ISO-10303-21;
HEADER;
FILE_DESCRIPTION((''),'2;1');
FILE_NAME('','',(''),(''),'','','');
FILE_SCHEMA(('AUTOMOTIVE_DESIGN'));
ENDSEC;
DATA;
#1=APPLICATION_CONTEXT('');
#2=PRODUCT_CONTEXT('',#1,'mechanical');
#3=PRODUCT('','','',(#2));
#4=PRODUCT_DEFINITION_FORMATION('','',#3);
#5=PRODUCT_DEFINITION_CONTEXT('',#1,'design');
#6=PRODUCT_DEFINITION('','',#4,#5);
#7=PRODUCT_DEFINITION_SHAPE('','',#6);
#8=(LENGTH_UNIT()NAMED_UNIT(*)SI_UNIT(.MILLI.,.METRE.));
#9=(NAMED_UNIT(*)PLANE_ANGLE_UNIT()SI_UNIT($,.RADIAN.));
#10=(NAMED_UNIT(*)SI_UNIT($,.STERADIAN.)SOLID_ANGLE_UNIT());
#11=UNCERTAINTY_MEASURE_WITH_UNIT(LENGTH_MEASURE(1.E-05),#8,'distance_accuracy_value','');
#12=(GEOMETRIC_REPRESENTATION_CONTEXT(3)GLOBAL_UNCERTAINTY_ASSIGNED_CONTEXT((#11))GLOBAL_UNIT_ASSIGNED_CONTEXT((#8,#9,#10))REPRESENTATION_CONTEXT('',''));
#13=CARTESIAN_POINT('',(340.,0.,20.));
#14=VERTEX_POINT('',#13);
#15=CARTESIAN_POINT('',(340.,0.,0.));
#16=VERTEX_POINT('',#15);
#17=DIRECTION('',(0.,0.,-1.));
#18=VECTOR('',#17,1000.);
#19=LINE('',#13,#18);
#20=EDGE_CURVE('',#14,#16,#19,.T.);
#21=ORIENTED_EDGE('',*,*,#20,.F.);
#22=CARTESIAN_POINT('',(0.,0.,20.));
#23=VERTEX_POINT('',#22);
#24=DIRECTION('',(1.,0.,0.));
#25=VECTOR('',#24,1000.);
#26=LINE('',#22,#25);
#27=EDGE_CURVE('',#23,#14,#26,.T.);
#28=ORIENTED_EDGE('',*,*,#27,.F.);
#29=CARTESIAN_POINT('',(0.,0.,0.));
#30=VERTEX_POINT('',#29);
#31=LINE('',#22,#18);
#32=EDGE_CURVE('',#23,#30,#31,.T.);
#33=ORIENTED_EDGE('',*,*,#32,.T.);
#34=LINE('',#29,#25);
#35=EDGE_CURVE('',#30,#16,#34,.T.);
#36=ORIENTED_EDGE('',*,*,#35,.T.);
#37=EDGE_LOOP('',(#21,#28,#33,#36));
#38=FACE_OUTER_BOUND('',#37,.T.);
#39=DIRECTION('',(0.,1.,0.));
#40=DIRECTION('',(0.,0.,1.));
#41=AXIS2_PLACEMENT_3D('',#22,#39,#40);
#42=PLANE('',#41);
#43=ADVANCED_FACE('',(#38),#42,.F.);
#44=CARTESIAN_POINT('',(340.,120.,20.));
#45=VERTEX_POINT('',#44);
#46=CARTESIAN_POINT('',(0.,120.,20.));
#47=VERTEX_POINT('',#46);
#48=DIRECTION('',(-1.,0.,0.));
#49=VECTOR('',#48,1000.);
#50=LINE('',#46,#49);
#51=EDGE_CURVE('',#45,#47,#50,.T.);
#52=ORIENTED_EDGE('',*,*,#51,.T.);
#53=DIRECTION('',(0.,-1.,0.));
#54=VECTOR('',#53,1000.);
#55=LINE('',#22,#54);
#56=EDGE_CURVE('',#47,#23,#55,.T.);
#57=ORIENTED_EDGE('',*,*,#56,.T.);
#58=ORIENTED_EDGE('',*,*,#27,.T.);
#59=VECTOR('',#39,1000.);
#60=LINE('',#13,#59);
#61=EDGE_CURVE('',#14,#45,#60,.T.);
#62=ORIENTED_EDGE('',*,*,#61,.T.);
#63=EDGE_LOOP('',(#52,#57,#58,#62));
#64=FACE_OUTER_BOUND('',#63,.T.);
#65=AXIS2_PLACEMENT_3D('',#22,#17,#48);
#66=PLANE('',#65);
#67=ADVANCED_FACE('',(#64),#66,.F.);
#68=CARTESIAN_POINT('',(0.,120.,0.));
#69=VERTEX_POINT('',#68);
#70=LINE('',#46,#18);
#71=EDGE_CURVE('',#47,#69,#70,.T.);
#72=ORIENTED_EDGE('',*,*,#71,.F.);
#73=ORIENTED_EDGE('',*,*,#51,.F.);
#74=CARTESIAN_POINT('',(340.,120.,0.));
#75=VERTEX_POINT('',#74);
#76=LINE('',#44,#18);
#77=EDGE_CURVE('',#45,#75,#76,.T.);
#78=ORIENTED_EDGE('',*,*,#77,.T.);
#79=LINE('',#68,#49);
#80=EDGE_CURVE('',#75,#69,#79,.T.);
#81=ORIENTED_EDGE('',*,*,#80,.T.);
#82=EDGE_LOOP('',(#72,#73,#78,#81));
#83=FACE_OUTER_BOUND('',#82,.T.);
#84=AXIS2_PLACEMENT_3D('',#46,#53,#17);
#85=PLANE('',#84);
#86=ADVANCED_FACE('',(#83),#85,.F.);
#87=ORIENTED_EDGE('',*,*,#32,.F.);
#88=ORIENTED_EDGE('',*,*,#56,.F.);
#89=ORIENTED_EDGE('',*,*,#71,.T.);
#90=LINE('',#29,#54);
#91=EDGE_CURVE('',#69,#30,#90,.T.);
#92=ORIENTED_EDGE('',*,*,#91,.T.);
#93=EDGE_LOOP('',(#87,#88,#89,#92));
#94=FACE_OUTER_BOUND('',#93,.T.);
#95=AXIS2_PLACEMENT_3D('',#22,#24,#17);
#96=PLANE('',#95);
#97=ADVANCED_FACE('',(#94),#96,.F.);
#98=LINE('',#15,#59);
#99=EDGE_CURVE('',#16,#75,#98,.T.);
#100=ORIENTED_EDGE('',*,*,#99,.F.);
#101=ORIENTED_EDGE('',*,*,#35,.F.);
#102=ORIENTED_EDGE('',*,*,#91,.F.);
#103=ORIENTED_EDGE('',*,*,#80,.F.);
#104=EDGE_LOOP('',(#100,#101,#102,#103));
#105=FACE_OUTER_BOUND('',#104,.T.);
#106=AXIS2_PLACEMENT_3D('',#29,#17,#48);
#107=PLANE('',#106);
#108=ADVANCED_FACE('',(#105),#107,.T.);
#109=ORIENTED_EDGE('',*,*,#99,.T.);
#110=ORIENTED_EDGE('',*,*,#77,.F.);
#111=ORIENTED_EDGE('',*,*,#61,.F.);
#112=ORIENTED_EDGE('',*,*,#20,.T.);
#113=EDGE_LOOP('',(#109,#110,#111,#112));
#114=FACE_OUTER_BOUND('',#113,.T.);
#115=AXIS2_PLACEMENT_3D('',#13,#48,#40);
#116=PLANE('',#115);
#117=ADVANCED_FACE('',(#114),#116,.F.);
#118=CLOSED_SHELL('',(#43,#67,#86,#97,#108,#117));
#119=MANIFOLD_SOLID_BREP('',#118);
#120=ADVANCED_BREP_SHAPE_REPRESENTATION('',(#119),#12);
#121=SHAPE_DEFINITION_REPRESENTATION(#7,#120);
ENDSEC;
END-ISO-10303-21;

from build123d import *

# Parameters (mm, degrees)
SKETCH1_W           = 340
SKETCH1_H           = 120
BOSS_EXTRUDE1_DEPTH = 20


with BuildPart() as part:
    # Sketch1 → Boss-Extrude1 (new body)
    with BuildSketch(Plane.XY):
        with Locations((170, 60)):
            Rectangle(SKETCH1_W, SKETCH1_H)
    extrude(amount=BOSS_EXTRUDE1_DEPTH)


solid = part.part
